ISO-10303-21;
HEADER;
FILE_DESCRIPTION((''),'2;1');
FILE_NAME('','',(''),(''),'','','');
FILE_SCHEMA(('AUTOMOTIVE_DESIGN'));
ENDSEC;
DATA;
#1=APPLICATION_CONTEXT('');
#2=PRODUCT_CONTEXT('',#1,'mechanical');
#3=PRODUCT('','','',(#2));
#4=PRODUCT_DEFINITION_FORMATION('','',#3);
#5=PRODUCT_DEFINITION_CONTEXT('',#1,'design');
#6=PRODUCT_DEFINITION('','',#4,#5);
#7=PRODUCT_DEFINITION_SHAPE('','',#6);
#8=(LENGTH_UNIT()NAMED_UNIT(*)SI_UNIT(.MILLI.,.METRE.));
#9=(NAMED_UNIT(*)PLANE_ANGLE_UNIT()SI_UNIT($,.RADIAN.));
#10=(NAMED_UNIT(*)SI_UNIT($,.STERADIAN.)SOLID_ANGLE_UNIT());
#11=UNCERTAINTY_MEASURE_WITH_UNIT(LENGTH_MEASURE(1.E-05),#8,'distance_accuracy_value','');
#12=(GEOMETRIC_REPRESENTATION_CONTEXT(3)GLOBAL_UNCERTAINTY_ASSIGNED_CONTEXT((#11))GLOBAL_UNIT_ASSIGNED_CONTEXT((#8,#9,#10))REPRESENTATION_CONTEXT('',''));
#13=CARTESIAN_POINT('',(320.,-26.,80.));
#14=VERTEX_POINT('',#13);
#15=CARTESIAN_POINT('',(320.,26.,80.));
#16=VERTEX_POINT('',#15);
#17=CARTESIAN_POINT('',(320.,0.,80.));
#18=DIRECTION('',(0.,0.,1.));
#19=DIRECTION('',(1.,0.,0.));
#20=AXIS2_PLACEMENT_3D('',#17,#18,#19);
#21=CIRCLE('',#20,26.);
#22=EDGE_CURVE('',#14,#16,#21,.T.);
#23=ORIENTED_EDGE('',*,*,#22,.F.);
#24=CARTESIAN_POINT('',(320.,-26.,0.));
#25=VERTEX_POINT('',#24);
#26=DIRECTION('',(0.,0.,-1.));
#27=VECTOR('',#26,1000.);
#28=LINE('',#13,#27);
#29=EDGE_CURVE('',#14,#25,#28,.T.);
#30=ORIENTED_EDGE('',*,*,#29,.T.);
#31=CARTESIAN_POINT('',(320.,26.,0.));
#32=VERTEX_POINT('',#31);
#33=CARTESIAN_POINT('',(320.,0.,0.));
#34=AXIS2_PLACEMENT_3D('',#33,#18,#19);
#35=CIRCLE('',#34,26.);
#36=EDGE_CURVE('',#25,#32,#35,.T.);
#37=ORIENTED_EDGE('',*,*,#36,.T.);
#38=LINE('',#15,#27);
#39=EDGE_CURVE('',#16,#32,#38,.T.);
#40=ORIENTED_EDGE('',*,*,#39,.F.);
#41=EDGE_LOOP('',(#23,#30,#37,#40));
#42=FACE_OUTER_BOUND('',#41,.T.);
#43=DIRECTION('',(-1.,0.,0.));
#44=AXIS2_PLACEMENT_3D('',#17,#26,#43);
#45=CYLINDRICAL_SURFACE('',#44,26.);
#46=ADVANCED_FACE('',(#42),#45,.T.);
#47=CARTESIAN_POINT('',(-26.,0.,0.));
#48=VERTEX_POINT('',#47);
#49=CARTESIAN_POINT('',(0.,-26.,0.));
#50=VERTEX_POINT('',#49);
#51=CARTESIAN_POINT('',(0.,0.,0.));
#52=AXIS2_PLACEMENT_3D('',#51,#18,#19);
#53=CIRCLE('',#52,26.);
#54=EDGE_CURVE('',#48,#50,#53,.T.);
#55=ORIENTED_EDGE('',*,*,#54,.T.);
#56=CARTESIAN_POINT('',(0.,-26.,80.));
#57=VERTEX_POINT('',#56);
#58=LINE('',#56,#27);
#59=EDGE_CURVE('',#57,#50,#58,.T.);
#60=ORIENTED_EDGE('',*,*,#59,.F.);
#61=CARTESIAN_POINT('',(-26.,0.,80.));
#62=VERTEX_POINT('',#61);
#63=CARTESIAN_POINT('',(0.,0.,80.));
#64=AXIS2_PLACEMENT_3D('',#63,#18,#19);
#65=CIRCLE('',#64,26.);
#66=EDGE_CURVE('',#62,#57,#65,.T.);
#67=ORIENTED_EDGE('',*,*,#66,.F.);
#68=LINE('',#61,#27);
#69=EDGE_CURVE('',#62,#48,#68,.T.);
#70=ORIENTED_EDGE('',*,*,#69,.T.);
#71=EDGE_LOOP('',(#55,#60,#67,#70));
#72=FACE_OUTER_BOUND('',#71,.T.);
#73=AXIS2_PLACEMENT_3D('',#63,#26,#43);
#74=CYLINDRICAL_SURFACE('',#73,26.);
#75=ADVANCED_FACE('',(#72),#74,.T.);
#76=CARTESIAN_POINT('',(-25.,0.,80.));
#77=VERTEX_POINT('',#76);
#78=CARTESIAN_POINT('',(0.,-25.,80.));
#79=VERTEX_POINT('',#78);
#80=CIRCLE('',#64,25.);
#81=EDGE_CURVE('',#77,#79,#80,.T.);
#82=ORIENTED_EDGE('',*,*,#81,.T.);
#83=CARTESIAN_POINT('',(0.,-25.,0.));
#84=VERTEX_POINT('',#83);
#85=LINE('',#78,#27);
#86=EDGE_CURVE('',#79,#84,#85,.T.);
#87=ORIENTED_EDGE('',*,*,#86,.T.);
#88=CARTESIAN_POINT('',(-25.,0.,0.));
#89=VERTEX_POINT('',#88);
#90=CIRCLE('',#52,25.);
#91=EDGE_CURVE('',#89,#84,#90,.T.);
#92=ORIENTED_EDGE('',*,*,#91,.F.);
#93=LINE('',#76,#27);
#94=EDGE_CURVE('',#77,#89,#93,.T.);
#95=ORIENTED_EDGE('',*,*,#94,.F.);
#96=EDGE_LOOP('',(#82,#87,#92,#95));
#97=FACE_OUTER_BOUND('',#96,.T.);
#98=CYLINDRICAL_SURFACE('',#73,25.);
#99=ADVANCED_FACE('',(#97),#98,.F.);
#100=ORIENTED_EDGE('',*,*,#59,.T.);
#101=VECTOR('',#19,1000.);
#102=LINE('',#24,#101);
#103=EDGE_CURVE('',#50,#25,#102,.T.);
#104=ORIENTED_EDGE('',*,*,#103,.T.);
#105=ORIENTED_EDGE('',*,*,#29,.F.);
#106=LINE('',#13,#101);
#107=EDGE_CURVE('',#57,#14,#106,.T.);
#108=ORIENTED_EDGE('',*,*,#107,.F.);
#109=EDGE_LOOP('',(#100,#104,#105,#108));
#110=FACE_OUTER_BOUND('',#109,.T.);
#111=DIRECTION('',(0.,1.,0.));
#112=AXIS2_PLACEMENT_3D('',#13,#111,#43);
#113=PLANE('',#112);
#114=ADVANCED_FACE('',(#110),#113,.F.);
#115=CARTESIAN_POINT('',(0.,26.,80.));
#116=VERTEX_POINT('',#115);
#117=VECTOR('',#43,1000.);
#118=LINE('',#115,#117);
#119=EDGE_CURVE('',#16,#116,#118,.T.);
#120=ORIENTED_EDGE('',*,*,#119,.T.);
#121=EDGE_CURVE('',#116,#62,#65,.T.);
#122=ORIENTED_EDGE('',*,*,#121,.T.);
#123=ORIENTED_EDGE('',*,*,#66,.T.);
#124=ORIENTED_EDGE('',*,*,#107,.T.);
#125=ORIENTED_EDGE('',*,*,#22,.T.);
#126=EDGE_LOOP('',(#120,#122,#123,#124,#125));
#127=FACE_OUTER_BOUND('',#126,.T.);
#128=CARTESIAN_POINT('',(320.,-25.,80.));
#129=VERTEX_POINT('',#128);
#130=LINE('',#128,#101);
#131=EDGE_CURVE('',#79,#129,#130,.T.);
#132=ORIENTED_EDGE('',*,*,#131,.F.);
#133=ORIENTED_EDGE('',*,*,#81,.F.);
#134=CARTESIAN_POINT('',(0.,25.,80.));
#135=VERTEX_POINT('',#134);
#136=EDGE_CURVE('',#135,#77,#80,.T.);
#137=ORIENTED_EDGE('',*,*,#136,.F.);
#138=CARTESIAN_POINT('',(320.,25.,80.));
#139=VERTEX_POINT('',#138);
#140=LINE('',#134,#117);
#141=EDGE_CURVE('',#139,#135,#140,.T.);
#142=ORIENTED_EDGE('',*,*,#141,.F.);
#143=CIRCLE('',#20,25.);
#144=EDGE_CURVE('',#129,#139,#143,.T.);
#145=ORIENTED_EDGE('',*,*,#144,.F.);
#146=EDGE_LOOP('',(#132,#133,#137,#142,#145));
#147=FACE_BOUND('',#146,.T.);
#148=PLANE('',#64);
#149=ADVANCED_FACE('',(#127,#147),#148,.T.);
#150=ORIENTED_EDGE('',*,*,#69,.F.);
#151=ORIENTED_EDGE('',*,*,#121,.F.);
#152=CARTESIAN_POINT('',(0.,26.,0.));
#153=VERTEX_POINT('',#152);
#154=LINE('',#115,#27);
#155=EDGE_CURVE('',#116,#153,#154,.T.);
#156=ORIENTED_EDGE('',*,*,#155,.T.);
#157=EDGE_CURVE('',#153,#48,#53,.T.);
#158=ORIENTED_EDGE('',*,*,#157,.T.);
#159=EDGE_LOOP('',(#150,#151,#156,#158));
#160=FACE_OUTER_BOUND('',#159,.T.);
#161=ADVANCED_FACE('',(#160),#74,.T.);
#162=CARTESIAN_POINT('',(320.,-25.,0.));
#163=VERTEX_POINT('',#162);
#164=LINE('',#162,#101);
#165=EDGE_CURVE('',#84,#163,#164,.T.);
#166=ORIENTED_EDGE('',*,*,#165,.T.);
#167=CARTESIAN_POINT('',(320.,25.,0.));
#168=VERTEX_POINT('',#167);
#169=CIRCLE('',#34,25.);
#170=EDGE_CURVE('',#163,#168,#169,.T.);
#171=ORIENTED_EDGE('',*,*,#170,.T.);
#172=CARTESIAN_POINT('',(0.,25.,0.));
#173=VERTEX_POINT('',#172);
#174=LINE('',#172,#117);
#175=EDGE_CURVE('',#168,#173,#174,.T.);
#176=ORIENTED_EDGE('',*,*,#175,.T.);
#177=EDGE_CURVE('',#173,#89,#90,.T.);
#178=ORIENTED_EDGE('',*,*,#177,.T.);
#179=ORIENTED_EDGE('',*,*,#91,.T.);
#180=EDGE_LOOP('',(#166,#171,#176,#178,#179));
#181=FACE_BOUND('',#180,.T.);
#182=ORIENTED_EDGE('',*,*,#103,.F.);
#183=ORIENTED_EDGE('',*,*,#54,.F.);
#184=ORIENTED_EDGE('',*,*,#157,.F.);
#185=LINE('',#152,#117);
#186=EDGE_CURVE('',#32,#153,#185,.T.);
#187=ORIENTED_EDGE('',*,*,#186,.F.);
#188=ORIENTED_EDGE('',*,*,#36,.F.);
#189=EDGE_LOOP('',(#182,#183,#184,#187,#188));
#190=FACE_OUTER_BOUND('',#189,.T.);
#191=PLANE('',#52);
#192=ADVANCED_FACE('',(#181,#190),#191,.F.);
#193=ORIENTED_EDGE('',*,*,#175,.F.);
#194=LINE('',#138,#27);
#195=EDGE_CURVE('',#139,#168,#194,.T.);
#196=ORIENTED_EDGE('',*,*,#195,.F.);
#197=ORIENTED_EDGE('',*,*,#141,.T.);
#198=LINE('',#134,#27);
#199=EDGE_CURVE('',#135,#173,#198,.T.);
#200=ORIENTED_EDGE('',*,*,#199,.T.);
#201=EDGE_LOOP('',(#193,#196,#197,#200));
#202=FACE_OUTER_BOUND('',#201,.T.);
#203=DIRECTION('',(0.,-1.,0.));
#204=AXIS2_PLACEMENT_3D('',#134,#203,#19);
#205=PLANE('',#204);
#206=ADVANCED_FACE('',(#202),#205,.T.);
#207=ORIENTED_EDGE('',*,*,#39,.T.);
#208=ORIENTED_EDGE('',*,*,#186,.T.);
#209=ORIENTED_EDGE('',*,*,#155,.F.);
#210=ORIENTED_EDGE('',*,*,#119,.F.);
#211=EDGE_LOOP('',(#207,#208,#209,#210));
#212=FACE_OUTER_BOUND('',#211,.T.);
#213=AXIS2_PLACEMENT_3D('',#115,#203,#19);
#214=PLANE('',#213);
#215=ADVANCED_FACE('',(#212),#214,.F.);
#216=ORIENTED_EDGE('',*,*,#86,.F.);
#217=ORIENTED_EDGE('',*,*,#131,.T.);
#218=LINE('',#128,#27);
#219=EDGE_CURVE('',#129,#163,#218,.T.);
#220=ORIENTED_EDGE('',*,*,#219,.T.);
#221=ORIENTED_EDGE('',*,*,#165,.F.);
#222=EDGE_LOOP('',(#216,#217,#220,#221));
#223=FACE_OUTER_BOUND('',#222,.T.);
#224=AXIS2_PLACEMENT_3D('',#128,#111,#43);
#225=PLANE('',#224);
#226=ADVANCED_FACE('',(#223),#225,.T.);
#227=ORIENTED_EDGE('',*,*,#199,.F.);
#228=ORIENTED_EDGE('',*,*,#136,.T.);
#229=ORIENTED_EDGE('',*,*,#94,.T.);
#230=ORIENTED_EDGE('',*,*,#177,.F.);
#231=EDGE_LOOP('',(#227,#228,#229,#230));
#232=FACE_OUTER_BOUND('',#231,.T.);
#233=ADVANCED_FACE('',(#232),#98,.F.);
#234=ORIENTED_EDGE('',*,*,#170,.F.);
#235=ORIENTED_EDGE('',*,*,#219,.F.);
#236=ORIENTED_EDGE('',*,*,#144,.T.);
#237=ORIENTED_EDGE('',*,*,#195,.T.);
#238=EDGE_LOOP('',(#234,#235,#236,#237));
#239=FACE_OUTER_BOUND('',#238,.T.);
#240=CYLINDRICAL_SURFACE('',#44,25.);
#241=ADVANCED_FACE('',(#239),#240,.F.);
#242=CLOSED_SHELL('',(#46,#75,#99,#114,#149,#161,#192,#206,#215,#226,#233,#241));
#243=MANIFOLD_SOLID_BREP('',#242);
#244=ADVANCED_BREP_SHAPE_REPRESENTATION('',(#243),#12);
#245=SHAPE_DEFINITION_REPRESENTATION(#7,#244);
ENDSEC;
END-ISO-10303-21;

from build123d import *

# Parameters (mm, degrees)
BOSS_EXTRUDE1_DEPTH = 80


with BuildPart() as part:
    # Sketch1 → Boss-Extrude1 (new body)
    with BuildSketch(Plane.XY):
        with BuildLine():
            Line((320, -26), (0, -26))
            ThreePointArc((0, -26), (-26, 0), (0, 26))
            Line((0, 26), (320, 26))
            ThreePointArc((320, 26), (346, 0), (320, -26))
        make_face()
        with BuildLine():
            Line((0, 25), (320, 25))
            ThreePointArc((320, 25), (345, 0), (320, -25))
            Line((320, -25), (0, -25))
            ThreePointArc((0, -25), (-25, 0), (0, 25))
        make_face(mode=Mode.SUBTRACT)
    extrude(amount=BOSS_EXTRUDE1_DEPTH)


solid = part.part
